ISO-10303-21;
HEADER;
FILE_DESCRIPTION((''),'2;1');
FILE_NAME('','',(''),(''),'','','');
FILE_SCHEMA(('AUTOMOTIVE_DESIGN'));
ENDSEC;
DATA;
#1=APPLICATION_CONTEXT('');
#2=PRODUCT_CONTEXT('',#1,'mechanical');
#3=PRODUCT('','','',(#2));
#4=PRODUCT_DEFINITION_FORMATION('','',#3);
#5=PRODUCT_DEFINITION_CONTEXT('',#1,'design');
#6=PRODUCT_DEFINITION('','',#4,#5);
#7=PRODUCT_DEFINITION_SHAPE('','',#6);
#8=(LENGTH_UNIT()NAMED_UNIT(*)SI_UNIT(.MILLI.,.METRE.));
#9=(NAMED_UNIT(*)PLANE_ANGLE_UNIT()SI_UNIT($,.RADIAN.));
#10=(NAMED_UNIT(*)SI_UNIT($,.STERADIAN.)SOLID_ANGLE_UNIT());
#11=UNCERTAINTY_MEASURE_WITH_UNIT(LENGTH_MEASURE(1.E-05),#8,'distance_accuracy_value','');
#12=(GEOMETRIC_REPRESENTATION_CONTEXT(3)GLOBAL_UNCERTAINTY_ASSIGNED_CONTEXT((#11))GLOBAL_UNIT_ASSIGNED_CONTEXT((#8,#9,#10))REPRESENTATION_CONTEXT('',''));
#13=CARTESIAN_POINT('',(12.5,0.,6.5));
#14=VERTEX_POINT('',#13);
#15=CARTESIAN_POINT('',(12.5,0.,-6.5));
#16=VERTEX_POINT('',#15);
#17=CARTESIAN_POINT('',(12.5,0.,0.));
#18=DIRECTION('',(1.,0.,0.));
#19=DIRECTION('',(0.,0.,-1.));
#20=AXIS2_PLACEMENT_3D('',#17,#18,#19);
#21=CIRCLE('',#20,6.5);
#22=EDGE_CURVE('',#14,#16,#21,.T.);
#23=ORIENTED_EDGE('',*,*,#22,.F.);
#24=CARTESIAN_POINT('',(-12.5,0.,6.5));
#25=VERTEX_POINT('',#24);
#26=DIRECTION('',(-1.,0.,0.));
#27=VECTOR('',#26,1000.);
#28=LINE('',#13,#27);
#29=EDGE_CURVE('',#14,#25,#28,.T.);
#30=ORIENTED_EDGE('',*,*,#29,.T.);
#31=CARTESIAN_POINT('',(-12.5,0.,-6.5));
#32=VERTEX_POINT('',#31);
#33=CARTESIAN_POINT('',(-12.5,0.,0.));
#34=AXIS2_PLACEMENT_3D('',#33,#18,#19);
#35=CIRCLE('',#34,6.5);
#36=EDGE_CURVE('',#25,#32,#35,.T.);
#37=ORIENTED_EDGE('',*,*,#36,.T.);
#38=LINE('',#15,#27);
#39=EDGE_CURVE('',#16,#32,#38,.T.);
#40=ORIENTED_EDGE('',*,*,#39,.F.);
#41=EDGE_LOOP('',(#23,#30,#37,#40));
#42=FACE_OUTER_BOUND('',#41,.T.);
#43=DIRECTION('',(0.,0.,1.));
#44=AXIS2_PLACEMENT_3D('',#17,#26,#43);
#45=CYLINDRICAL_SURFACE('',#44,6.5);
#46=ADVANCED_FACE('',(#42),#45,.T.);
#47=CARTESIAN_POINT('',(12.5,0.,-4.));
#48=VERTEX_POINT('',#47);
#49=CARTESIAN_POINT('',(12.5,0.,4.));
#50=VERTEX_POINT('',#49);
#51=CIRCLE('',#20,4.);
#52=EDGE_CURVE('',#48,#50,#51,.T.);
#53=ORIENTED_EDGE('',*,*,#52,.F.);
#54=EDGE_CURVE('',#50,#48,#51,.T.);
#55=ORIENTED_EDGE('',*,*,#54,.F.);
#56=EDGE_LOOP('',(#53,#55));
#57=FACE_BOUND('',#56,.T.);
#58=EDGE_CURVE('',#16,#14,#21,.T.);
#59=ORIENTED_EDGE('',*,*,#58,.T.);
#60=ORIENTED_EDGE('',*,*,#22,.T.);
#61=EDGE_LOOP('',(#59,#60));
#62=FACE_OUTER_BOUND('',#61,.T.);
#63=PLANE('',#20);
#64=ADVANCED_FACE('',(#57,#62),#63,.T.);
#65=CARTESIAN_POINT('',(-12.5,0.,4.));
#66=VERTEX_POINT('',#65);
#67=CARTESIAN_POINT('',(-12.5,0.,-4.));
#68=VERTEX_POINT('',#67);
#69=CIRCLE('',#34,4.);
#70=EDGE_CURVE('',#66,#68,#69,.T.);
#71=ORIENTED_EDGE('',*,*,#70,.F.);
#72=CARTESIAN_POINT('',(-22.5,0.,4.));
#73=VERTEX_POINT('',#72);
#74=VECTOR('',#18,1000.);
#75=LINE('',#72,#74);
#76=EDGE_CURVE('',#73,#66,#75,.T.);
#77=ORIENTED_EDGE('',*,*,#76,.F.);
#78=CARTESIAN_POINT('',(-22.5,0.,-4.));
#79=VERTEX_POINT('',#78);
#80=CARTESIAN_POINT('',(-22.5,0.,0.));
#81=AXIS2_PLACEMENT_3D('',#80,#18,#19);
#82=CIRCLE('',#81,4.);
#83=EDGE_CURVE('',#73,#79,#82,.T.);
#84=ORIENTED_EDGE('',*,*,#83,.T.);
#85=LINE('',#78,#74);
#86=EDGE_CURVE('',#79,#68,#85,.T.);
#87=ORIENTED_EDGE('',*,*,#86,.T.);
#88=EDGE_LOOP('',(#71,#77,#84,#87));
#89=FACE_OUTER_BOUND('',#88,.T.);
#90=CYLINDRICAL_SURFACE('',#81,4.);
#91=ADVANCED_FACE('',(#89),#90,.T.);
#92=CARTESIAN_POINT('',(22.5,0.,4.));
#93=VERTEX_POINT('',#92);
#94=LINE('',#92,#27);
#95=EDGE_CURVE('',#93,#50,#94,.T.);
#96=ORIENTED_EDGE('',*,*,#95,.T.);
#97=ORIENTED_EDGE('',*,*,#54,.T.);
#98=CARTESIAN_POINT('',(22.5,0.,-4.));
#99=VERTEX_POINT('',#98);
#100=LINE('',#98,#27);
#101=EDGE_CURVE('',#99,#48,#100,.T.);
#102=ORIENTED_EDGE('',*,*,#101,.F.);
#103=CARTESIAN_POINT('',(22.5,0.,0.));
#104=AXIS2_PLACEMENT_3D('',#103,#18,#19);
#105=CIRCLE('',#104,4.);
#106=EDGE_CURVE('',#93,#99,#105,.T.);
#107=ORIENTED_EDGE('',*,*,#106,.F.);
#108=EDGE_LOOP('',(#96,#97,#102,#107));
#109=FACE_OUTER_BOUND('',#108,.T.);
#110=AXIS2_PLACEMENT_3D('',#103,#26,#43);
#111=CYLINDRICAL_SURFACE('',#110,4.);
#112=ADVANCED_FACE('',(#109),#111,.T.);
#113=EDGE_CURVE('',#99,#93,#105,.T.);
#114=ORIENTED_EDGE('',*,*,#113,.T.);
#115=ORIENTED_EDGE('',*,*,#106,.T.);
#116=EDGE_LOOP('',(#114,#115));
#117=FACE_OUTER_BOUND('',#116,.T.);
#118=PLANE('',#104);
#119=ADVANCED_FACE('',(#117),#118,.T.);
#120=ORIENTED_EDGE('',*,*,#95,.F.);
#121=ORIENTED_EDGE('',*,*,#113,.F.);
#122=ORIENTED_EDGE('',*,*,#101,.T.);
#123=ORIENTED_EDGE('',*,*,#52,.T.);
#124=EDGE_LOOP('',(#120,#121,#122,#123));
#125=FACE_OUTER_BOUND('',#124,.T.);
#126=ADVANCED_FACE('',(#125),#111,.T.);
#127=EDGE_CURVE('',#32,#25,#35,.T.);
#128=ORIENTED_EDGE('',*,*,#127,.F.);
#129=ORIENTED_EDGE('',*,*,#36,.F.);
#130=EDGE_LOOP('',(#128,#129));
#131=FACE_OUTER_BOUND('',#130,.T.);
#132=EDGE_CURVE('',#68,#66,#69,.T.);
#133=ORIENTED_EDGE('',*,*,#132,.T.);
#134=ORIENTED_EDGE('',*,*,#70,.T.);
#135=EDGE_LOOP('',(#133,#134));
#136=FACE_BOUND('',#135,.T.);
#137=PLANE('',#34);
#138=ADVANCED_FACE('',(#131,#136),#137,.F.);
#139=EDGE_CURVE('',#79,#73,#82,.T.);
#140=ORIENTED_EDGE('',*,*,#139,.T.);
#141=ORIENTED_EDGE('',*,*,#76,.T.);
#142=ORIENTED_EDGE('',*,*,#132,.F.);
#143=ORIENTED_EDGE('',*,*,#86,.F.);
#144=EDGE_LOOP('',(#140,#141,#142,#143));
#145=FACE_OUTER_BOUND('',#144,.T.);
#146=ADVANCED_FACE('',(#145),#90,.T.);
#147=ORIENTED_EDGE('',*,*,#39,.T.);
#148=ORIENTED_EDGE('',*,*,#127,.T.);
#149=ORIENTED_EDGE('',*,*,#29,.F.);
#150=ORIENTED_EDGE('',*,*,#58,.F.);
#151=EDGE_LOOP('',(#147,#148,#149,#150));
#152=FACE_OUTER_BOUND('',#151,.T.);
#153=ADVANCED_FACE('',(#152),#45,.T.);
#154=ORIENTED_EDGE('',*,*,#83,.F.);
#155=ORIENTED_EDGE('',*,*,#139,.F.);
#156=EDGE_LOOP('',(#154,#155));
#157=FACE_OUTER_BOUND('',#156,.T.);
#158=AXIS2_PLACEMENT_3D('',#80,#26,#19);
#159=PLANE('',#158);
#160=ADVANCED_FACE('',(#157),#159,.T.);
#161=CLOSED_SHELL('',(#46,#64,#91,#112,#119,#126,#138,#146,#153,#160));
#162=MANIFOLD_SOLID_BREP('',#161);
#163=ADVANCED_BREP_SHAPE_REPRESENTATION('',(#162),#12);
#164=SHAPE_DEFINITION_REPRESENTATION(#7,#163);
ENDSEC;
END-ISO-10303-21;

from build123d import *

# Parameters (mm, degrees)
SKETCH1_R           = 6.5
BOSS_EXTRUDE1_DEPTH = 12.5
SKETCH3_R           = 4
BOSS_EXTRUDE2_DEPTH = 10


with BuildPart() as part:
    # Sketch1 → Boss-Extrude1 (new, symmetric)
    with BuildSketch(Plane(origin=(0, 0, 0), x_dir=(0, 0, -1), z_dir=(1, 0, 0))):
        Circle(SKETCH1_R)
    extrude(amount=BOSS_EXTRUDE1_DEPTH, both=True)

    # Sketch3 → Boss-Extrude2 (add)
    with BuildSketch(Plane(origin=(12.5, 0, 0), x_dir=(0, 0, -1), z_dir=(1, 0, 0))):
        Circle(SKETCH3_R)
    boss_extrude2 = extrude(amount=BOSS_EXTRUDE2_DEPTH)

    # Mirror1: Boss-Extrude2 across plane
    add(boss_extrude2.mirror(Plane(origin=(0, 0, 0), x_dir=(0, 0, 1), z_dir=(1, 0, 0))))


solid = part.part
